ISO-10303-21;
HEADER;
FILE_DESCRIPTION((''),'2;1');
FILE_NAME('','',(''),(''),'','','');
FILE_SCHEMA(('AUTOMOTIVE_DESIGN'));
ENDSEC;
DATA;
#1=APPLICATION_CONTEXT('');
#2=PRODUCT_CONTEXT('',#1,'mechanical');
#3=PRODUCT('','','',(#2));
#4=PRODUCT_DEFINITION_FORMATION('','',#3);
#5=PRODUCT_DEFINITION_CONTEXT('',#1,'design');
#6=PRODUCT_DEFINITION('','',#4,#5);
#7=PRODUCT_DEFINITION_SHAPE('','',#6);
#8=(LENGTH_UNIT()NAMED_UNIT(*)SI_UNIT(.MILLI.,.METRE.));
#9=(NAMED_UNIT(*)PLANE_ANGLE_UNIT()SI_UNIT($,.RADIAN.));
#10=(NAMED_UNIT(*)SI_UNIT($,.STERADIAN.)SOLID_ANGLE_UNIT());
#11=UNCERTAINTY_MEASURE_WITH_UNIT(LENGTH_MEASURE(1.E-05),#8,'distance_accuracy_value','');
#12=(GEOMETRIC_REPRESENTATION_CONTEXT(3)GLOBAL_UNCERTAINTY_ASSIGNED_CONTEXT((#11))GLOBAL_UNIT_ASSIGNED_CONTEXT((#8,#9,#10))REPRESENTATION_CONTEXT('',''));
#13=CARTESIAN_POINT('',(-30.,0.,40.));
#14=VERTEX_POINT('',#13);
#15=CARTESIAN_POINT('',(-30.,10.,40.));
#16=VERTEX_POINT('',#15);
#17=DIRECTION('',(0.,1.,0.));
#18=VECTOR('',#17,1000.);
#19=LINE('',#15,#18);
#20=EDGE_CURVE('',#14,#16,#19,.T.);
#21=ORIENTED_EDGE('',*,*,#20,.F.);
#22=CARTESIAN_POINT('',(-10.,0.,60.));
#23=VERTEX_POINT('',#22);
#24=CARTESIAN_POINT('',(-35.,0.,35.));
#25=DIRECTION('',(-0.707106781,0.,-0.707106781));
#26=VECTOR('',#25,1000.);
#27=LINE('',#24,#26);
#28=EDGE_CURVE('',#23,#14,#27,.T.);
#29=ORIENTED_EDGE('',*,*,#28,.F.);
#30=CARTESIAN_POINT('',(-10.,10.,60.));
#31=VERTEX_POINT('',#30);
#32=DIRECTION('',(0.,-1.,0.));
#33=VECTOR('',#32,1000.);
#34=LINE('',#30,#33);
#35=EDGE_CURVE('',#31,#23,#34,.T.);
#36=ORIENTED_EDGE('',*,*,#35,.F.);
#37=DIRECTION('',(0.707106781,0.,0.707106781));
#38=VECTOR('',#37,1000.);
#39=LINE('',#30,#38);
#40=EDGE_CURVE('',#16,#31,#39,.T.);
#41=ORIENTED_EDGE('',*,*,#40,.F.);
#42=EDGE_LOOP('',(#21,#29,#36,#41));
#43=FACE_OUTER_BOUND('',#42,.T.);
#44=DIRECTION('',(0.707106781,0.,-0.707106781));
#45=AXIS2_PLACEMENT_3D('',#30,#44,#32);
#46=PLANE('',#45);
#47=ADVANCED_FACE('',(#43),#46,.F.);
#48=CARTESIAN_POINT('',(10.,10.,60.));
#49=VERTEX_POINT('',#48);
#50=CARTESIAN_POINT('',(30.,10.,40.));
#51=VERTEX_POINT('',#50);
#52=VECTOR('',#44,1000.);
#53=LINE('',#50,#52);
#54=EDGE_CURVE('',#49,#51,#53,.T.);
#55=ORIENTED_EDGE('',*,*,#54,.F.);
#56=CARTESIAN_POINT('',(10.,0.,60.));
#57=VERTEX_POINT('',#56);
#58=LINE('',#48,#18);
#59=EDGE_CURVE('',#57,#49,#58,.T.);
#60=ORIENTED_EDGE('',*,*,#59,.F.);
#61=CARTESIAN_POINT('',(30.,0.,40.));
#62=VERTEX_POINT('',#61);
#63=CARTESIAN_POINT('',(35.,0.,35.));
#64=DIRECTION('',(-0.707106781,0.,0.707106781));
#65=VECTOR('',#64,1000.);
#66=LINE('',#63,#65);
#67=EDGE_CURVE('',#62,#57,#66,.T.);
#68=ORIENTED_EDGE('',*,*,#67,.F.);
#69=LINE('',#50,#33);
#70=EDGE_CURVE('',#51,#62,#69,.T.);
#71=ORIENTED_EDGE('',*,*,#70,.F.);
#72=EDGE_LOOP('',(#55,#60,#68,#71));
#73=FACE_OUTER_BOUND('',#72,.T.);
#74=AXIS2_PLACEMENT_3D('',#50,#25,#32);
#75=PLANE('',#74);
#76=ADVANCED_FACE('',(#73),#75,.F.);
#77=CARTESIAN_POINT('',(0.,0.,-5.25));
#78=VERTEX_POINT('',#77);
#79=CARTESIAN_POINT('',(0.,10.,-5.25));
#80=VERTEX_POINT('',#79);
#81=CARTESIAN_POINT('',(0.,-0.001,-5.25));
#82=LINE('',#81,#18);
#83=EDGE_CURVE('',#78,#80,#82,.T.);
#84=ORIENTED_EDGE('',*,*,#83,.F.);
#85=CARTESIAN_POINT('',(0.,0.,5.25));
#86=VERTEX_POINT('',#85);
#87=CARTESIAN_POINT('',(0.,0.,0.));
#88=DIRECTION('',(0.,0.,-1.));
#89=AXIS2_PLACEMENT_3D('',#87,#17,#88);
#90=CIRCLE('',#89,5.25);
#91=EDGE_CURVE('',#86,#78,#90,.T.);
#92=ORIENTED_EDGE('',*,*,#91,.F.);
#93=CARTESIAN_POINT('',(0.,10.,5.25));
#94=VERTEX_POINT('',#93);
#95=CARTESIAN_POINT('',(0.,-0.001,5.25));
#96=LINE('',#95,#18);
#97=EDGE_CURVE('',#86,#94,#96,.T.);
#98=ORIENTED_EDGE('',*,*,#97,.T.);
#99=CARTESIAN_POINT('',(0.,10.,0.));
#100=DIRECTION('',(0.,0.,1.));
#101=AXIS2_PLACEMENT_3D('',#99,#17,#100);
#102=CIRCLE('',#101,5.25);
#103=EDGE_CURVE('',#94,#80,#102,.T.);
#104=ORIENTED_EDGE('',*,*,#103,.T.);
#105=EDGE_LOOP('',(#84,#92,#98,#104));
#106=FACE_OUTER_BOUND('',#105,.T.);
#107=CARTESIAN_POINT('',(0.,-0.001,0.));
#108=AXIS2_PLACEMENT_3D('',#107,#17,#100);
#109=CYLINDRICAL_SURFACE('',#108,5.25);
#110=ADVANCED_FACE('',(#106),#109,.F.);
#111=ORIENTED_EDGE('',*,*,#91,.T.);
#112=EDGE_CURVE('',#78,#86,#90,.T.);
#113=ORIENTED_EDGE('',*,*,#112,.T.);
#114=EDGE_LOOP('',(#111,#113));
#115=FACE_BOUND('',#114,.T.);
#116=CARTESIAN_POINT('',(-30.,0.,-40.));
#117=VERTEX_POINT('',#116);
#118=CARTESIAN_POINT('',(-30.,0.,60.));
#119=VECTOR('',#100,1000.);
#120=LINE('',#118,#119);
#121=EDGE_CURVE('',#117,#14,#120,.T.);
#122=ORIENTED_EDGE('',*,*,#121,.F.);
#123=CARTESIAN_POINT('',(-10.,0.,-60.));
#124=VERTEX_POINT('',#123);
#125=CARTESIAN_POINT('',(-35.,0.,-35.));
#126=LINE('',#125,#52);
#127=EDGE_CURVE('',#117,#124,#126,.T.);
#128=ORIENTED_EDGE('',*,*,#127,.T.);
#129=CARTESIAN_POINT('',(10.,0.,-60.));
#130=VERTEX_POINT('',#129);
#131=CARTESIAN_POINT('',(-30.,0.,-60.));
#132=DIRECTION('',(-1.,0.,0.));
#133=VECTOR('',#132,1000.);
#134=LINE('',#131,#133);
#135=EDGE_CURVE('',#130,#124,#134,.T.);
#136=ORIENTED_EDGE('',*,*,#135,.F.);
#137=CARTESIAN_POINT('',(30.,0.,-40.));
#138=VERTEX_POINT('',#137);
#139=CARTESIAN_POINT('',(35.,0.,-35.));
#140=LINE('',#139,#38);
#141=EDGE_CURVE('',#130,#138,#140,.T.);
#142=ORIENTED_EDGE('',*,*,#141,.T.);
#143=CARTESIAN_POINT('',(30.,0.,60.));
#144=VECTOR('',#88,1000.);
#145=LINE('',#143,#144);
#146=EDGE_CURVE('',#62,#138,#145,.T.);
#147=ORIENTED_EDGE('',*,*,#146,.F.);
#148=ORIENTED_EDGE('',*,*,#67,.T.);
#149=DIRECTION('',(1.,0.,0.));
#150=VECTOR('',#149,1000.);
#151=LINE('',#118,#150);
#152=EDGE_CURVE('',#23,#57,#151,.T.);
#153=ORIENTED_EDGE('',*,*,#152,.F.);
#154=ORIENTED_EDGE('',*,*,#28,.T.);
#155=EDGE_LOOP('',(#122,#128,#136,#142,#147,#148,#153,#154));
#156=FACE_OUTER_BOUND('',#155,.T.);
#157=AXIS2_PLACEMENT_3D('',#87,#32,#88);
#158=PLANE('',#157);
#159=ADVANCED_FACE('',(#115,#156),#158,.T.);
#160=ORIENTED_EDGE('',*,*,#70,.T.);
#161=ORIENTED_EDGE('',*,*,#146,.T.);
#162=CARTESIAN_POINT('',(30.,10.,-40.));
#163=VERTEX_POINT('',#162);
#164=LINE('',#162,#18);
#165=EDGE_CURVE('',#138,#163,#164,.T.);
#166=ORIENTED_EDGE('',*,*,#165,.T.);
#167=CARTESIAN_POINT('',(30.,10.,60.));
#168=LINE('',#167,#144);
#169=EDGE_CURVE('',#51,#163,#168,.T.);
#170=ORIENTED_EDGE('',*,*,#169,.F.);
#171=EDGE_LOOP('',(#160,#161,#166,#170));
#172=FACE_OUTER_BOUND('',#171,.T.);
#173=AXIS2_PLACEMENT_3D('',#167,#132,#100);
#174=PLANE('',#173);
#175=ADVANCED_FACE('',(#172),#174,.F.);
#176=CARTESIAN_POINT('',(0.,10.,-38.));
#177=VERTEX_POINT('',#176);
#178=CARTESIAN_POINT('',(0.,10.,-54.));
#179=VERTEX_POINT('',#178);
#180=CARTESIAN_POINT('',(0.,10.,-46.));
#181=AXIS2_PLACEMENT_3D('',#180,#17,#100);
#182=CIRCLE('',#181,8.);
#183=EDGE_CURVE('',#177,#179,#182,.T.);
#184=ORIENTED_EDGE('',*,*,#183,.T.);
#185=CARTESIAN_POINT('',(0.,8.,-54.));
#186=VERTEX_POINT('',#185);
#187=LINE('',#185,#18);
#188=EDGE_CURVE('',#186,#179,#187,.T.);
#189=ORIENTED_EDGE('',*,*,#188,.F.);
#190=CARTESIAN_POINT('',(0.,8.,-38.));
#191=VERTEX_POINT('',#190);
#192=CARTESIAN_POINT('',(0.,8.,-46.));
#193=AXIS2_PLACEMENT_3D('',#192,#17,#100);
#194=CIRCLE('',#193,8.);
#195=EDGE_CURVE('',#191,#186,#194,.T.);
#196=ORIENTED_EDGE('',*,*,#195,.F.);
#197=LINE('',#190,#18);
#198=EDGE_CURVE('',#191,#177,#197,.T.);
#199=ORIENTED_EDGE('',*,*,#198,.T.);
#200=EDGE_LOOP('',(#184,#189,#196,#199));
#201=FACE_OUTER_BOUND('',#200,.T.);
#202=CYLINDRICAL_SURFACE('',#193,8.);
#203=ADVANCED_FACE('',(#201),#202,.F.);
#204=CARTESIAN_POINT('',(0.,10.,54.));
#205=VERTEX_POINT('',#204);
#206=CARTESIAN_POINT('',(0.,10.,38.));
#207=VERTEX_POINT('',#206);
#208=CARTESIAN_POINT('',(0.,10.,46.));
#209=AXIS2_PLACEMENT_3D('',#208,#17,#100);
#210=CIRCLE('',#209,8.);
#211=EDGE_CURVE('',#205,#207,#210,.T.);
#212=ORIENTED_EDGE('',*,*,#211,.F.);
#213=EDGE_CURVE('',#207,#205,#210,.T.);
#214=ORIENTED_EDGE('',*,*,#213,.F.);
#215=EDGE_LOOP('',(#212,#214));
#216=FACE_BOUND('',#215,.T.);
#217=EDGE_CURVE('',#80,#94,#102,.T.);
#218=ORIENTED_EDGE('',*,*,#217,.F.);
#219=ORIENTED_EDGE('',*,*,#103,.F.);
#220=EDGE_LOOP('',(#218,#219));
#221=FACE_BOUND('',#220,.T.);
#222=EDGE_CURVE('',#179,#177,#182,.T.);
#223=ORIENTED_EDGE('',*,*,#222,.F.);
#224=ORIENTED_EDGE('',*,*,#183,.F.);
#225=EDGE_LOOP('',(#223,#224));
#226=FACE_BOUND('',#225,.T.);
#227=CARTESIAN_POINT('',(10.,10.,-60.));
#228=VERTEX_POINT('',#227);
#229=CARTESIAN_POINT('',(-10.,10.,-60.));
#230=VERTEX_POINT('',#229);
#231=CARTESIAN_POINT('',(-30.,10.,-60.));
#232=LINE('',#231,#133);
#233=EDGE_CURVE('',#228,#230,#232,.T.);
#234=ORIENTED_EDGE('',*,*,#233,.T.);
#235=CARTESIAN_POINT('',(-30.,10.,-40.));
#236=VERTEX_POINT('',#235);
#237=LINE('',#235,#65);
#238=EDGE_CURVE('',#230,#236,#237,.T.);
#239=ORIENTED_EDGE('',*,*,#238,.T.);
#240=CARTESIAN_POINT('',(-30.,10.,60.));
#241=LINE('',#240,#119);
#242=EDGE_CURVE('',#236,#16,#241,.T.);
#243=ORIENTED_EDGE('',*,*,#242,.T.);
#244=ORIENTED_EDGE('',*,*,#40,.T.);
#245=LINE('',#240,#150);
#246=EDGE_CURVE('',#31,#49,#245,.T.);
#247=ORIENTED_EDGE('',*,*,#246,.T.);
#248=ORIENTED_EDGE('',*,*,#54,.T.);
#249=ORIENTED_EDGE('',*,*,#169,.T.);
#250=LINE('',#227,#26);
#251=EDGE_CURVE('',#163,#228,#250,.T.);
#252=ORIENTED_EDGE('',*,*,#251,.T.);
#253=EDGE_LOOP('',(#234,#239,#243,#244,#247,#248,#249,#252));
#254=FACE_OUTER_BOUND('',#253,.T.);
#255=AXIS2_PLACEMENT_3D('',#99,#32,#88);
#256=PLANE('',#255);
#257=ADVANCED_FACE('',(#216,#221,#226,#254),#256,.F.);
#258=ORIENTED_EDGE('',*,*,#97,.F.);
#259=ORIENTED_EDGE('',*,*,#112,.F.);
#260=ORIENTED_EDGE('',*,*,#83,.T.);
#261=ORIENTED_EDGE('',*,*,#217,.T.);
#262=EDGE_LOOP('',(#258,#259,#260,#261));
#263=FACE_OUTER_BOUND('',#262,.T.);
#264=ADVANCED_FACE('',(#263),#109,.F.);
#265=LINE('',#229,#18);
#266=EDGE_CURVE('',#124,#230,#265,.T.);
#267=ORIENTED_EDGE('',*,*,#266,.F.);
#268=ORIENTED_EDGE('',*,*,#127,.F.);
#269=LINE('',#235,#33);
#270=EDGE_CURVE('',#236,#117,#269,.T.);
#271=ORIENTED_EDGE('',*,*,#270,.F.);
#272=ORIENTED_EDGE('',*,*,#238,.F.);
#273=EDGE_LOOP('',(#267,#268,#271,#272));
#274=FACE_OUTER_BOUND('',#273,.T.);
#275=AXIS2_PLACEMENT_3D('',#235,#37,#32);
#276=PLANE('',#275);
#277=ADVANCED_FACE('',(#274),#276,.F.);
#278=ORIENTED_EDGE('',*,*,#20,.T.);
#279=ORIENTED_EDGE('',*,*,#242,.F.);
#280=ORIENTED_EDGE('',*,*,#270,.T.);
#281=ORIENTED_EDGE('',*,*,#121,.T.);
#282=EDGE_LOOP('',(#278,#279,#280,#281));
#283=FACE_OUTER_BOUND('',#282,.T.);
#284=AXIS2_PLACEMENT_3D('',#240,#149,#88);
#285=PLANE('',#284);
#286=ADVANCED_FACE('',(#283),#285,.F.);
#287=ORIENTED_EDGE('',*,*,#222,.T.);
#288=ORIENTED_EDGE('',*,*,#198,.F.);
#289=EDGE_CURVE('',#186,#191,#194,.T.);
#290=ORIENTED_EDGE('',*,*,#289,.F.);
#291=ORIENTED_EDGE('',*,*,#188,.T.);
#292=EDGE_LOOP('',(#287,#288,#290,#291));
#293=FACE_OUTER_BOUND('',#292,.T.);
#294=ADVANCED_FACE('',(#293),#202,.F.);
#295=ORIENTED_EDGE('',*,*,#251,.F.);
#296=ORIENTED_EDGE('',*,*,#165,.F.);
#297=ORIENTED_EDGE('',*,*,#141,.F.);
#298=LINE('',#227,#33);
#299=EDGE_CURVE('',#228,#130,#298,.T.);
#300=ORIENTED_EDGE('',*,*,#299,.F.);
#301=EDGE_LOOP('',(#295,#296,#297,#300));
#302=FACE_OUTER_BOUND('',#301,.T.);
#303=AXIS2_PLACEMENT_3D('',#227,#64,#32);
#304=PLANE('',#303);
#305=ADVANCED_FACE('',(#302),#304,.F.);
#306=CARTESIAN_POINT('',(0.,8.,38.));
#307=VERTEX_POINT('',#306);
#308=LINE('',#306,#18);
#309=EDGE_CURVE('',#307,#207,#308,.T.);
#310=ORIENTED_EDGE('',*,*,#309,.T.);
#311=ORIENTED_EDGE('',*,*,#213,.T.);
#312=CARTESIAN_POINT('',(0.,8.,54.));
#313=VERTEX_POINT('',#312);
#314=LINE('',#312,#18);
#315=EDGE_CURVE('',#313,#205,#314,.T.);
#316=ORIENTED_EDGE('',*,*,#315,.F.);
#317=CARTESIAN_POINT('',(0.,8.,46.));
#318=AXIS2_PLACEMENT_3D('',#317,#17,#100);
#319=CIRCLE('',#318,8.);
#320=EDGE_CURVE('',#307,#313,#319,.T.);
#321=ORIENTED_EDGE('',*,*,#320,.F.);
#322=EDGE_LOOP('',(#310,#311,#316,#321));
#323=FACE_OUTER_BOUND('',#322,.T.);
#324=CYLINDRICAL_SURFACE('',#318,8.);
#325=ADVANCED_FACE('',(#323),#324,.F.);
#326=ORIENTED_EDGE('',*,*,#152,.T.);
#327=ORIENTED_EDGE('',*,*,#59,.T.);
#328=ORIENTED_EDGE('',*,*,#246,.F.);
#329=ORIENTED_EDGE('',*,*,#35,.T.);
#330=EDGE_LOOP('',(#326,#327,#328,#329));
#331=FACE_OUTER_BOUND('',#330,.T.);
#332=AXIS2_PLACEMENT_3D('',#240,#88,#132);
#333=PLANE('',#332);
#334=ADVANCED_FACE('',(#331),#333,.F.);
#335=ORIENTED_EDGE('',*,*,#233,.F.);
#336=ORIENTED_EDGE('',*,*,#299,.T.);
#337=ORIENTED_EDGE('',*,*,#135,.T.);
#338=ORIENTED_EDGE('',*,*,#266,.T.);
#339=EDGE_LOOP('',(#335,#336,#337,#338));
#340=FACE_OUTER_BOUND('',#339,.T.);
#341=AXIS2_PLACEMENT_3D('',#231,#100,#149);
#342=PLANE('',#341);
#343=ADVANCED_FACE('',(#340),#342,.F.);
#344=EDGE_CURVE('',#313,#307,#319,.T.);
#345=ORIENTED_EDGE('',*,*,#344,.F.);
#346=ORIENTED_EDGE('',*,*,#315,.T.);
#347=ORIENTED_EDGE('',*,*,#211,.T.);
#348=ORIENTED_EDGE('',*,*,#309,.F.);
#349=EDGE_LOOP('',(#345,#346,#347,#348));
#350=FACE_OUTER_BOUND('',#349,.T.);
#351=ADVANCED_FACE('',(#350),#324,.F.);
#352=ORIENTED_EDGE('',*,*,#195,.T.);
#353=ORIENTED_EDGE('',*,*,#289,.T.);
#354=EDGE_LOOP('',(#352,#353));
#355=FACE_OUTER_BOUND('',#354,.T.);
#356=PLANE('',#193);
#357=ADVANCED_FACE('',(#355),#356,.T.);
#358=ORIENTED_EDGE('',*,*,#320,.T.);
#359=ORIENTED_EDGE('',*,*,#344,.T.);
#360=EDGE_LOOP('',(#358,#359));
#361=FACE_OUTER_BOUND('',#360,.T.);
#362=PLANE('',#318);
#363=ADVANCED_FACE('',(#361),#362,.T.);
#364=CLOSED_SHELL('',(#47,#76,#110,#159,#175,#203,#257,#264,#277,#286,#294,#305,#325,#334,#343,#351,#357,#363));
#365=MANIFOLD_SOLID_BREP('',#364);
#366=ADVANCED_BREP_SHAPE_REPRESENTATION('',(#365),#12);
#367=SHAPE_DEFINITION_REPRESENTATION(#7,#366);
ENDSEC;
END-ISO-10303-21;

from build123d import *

# Parameters (mm, degrees)
SKETCH_1_W          = 60
SKETCH_1_H          = 120
EXTRUDE_1_DEPTH     = 10
SKETCH_2_R          = 8
CUT_EXTRUDE_1_DEPTH = 2
CHAMFER_1_SIZE      = 20
CUT_EXTRUDE_2_REACH = 69.823
SKETCH_3_R          = 5.25


with BuildPart() as part:
    # 草图1 → 凸台-拉伸1 (new body)
    with BuildSketch(Plane(origin=(0, 0, 0), x_dir=(1, 0, 0), z_dir=(0, 1, 0))):
        Rectangle(SKETCH_1_W, SKETCH_1_H)
    extrude(amount=EXTRUDE_1_DEPTH)

    # 草图2 → 切除-拉伸1 (cut)
    with BuildSketch(Plane(origin=(0, 10, 0), x_dir=(1, 0, 0), z_dir=(0, 1, 0))):
        with Locations(Location((0, 46, 0), (0, 0, 270))):
            Circle(SKETCH_2_R)
        with Locations(Location((0, -46, 0), (0, 0, 270))):
            Circle(SKETCH_2_R)
    extrude(amount=-CUT_EXTRUDE_1_DEPTH, mode=Mode.SUBTRACT)

    # 倒角1
    chamfer_1_edges = [part.edges().sort_by_distance(p)[0] for p in [
        (30, 5, 60),
        (-30, 5, 60),
        (-30, 5, -60),
        (30, 5, -60),
    ]]
    chamfer(chamfer_1_edges, length=CHAMFER_1_SIZE)

    # 草图3 → 切除-拉伸2 (cut, up to next)
    with BuildSketch(Plane(origin=(0, 10, 0), x_dir=(1, 0, 0), z_dir=(0, 1, 0)), mode=Mode.PRIVATE) as cut_extrude_2_sk1:
        with Locations(Location((0, 0, 0), (0, 0, 270))):
            Circle(SKETCH_3_R)
    cut_extrude_2_tool1 = extrude(cut_extrude_2_sk1.sketch, amount=-CUT_EXTRUDE_2_REACH, mode=Mode.PRIVATE) & part.part
    add(cut_extrude_2_tool1.solids().sort_by_distance((0, 10, 0))[0], mode=Mode.SUBTRACT)


solid = part.part
